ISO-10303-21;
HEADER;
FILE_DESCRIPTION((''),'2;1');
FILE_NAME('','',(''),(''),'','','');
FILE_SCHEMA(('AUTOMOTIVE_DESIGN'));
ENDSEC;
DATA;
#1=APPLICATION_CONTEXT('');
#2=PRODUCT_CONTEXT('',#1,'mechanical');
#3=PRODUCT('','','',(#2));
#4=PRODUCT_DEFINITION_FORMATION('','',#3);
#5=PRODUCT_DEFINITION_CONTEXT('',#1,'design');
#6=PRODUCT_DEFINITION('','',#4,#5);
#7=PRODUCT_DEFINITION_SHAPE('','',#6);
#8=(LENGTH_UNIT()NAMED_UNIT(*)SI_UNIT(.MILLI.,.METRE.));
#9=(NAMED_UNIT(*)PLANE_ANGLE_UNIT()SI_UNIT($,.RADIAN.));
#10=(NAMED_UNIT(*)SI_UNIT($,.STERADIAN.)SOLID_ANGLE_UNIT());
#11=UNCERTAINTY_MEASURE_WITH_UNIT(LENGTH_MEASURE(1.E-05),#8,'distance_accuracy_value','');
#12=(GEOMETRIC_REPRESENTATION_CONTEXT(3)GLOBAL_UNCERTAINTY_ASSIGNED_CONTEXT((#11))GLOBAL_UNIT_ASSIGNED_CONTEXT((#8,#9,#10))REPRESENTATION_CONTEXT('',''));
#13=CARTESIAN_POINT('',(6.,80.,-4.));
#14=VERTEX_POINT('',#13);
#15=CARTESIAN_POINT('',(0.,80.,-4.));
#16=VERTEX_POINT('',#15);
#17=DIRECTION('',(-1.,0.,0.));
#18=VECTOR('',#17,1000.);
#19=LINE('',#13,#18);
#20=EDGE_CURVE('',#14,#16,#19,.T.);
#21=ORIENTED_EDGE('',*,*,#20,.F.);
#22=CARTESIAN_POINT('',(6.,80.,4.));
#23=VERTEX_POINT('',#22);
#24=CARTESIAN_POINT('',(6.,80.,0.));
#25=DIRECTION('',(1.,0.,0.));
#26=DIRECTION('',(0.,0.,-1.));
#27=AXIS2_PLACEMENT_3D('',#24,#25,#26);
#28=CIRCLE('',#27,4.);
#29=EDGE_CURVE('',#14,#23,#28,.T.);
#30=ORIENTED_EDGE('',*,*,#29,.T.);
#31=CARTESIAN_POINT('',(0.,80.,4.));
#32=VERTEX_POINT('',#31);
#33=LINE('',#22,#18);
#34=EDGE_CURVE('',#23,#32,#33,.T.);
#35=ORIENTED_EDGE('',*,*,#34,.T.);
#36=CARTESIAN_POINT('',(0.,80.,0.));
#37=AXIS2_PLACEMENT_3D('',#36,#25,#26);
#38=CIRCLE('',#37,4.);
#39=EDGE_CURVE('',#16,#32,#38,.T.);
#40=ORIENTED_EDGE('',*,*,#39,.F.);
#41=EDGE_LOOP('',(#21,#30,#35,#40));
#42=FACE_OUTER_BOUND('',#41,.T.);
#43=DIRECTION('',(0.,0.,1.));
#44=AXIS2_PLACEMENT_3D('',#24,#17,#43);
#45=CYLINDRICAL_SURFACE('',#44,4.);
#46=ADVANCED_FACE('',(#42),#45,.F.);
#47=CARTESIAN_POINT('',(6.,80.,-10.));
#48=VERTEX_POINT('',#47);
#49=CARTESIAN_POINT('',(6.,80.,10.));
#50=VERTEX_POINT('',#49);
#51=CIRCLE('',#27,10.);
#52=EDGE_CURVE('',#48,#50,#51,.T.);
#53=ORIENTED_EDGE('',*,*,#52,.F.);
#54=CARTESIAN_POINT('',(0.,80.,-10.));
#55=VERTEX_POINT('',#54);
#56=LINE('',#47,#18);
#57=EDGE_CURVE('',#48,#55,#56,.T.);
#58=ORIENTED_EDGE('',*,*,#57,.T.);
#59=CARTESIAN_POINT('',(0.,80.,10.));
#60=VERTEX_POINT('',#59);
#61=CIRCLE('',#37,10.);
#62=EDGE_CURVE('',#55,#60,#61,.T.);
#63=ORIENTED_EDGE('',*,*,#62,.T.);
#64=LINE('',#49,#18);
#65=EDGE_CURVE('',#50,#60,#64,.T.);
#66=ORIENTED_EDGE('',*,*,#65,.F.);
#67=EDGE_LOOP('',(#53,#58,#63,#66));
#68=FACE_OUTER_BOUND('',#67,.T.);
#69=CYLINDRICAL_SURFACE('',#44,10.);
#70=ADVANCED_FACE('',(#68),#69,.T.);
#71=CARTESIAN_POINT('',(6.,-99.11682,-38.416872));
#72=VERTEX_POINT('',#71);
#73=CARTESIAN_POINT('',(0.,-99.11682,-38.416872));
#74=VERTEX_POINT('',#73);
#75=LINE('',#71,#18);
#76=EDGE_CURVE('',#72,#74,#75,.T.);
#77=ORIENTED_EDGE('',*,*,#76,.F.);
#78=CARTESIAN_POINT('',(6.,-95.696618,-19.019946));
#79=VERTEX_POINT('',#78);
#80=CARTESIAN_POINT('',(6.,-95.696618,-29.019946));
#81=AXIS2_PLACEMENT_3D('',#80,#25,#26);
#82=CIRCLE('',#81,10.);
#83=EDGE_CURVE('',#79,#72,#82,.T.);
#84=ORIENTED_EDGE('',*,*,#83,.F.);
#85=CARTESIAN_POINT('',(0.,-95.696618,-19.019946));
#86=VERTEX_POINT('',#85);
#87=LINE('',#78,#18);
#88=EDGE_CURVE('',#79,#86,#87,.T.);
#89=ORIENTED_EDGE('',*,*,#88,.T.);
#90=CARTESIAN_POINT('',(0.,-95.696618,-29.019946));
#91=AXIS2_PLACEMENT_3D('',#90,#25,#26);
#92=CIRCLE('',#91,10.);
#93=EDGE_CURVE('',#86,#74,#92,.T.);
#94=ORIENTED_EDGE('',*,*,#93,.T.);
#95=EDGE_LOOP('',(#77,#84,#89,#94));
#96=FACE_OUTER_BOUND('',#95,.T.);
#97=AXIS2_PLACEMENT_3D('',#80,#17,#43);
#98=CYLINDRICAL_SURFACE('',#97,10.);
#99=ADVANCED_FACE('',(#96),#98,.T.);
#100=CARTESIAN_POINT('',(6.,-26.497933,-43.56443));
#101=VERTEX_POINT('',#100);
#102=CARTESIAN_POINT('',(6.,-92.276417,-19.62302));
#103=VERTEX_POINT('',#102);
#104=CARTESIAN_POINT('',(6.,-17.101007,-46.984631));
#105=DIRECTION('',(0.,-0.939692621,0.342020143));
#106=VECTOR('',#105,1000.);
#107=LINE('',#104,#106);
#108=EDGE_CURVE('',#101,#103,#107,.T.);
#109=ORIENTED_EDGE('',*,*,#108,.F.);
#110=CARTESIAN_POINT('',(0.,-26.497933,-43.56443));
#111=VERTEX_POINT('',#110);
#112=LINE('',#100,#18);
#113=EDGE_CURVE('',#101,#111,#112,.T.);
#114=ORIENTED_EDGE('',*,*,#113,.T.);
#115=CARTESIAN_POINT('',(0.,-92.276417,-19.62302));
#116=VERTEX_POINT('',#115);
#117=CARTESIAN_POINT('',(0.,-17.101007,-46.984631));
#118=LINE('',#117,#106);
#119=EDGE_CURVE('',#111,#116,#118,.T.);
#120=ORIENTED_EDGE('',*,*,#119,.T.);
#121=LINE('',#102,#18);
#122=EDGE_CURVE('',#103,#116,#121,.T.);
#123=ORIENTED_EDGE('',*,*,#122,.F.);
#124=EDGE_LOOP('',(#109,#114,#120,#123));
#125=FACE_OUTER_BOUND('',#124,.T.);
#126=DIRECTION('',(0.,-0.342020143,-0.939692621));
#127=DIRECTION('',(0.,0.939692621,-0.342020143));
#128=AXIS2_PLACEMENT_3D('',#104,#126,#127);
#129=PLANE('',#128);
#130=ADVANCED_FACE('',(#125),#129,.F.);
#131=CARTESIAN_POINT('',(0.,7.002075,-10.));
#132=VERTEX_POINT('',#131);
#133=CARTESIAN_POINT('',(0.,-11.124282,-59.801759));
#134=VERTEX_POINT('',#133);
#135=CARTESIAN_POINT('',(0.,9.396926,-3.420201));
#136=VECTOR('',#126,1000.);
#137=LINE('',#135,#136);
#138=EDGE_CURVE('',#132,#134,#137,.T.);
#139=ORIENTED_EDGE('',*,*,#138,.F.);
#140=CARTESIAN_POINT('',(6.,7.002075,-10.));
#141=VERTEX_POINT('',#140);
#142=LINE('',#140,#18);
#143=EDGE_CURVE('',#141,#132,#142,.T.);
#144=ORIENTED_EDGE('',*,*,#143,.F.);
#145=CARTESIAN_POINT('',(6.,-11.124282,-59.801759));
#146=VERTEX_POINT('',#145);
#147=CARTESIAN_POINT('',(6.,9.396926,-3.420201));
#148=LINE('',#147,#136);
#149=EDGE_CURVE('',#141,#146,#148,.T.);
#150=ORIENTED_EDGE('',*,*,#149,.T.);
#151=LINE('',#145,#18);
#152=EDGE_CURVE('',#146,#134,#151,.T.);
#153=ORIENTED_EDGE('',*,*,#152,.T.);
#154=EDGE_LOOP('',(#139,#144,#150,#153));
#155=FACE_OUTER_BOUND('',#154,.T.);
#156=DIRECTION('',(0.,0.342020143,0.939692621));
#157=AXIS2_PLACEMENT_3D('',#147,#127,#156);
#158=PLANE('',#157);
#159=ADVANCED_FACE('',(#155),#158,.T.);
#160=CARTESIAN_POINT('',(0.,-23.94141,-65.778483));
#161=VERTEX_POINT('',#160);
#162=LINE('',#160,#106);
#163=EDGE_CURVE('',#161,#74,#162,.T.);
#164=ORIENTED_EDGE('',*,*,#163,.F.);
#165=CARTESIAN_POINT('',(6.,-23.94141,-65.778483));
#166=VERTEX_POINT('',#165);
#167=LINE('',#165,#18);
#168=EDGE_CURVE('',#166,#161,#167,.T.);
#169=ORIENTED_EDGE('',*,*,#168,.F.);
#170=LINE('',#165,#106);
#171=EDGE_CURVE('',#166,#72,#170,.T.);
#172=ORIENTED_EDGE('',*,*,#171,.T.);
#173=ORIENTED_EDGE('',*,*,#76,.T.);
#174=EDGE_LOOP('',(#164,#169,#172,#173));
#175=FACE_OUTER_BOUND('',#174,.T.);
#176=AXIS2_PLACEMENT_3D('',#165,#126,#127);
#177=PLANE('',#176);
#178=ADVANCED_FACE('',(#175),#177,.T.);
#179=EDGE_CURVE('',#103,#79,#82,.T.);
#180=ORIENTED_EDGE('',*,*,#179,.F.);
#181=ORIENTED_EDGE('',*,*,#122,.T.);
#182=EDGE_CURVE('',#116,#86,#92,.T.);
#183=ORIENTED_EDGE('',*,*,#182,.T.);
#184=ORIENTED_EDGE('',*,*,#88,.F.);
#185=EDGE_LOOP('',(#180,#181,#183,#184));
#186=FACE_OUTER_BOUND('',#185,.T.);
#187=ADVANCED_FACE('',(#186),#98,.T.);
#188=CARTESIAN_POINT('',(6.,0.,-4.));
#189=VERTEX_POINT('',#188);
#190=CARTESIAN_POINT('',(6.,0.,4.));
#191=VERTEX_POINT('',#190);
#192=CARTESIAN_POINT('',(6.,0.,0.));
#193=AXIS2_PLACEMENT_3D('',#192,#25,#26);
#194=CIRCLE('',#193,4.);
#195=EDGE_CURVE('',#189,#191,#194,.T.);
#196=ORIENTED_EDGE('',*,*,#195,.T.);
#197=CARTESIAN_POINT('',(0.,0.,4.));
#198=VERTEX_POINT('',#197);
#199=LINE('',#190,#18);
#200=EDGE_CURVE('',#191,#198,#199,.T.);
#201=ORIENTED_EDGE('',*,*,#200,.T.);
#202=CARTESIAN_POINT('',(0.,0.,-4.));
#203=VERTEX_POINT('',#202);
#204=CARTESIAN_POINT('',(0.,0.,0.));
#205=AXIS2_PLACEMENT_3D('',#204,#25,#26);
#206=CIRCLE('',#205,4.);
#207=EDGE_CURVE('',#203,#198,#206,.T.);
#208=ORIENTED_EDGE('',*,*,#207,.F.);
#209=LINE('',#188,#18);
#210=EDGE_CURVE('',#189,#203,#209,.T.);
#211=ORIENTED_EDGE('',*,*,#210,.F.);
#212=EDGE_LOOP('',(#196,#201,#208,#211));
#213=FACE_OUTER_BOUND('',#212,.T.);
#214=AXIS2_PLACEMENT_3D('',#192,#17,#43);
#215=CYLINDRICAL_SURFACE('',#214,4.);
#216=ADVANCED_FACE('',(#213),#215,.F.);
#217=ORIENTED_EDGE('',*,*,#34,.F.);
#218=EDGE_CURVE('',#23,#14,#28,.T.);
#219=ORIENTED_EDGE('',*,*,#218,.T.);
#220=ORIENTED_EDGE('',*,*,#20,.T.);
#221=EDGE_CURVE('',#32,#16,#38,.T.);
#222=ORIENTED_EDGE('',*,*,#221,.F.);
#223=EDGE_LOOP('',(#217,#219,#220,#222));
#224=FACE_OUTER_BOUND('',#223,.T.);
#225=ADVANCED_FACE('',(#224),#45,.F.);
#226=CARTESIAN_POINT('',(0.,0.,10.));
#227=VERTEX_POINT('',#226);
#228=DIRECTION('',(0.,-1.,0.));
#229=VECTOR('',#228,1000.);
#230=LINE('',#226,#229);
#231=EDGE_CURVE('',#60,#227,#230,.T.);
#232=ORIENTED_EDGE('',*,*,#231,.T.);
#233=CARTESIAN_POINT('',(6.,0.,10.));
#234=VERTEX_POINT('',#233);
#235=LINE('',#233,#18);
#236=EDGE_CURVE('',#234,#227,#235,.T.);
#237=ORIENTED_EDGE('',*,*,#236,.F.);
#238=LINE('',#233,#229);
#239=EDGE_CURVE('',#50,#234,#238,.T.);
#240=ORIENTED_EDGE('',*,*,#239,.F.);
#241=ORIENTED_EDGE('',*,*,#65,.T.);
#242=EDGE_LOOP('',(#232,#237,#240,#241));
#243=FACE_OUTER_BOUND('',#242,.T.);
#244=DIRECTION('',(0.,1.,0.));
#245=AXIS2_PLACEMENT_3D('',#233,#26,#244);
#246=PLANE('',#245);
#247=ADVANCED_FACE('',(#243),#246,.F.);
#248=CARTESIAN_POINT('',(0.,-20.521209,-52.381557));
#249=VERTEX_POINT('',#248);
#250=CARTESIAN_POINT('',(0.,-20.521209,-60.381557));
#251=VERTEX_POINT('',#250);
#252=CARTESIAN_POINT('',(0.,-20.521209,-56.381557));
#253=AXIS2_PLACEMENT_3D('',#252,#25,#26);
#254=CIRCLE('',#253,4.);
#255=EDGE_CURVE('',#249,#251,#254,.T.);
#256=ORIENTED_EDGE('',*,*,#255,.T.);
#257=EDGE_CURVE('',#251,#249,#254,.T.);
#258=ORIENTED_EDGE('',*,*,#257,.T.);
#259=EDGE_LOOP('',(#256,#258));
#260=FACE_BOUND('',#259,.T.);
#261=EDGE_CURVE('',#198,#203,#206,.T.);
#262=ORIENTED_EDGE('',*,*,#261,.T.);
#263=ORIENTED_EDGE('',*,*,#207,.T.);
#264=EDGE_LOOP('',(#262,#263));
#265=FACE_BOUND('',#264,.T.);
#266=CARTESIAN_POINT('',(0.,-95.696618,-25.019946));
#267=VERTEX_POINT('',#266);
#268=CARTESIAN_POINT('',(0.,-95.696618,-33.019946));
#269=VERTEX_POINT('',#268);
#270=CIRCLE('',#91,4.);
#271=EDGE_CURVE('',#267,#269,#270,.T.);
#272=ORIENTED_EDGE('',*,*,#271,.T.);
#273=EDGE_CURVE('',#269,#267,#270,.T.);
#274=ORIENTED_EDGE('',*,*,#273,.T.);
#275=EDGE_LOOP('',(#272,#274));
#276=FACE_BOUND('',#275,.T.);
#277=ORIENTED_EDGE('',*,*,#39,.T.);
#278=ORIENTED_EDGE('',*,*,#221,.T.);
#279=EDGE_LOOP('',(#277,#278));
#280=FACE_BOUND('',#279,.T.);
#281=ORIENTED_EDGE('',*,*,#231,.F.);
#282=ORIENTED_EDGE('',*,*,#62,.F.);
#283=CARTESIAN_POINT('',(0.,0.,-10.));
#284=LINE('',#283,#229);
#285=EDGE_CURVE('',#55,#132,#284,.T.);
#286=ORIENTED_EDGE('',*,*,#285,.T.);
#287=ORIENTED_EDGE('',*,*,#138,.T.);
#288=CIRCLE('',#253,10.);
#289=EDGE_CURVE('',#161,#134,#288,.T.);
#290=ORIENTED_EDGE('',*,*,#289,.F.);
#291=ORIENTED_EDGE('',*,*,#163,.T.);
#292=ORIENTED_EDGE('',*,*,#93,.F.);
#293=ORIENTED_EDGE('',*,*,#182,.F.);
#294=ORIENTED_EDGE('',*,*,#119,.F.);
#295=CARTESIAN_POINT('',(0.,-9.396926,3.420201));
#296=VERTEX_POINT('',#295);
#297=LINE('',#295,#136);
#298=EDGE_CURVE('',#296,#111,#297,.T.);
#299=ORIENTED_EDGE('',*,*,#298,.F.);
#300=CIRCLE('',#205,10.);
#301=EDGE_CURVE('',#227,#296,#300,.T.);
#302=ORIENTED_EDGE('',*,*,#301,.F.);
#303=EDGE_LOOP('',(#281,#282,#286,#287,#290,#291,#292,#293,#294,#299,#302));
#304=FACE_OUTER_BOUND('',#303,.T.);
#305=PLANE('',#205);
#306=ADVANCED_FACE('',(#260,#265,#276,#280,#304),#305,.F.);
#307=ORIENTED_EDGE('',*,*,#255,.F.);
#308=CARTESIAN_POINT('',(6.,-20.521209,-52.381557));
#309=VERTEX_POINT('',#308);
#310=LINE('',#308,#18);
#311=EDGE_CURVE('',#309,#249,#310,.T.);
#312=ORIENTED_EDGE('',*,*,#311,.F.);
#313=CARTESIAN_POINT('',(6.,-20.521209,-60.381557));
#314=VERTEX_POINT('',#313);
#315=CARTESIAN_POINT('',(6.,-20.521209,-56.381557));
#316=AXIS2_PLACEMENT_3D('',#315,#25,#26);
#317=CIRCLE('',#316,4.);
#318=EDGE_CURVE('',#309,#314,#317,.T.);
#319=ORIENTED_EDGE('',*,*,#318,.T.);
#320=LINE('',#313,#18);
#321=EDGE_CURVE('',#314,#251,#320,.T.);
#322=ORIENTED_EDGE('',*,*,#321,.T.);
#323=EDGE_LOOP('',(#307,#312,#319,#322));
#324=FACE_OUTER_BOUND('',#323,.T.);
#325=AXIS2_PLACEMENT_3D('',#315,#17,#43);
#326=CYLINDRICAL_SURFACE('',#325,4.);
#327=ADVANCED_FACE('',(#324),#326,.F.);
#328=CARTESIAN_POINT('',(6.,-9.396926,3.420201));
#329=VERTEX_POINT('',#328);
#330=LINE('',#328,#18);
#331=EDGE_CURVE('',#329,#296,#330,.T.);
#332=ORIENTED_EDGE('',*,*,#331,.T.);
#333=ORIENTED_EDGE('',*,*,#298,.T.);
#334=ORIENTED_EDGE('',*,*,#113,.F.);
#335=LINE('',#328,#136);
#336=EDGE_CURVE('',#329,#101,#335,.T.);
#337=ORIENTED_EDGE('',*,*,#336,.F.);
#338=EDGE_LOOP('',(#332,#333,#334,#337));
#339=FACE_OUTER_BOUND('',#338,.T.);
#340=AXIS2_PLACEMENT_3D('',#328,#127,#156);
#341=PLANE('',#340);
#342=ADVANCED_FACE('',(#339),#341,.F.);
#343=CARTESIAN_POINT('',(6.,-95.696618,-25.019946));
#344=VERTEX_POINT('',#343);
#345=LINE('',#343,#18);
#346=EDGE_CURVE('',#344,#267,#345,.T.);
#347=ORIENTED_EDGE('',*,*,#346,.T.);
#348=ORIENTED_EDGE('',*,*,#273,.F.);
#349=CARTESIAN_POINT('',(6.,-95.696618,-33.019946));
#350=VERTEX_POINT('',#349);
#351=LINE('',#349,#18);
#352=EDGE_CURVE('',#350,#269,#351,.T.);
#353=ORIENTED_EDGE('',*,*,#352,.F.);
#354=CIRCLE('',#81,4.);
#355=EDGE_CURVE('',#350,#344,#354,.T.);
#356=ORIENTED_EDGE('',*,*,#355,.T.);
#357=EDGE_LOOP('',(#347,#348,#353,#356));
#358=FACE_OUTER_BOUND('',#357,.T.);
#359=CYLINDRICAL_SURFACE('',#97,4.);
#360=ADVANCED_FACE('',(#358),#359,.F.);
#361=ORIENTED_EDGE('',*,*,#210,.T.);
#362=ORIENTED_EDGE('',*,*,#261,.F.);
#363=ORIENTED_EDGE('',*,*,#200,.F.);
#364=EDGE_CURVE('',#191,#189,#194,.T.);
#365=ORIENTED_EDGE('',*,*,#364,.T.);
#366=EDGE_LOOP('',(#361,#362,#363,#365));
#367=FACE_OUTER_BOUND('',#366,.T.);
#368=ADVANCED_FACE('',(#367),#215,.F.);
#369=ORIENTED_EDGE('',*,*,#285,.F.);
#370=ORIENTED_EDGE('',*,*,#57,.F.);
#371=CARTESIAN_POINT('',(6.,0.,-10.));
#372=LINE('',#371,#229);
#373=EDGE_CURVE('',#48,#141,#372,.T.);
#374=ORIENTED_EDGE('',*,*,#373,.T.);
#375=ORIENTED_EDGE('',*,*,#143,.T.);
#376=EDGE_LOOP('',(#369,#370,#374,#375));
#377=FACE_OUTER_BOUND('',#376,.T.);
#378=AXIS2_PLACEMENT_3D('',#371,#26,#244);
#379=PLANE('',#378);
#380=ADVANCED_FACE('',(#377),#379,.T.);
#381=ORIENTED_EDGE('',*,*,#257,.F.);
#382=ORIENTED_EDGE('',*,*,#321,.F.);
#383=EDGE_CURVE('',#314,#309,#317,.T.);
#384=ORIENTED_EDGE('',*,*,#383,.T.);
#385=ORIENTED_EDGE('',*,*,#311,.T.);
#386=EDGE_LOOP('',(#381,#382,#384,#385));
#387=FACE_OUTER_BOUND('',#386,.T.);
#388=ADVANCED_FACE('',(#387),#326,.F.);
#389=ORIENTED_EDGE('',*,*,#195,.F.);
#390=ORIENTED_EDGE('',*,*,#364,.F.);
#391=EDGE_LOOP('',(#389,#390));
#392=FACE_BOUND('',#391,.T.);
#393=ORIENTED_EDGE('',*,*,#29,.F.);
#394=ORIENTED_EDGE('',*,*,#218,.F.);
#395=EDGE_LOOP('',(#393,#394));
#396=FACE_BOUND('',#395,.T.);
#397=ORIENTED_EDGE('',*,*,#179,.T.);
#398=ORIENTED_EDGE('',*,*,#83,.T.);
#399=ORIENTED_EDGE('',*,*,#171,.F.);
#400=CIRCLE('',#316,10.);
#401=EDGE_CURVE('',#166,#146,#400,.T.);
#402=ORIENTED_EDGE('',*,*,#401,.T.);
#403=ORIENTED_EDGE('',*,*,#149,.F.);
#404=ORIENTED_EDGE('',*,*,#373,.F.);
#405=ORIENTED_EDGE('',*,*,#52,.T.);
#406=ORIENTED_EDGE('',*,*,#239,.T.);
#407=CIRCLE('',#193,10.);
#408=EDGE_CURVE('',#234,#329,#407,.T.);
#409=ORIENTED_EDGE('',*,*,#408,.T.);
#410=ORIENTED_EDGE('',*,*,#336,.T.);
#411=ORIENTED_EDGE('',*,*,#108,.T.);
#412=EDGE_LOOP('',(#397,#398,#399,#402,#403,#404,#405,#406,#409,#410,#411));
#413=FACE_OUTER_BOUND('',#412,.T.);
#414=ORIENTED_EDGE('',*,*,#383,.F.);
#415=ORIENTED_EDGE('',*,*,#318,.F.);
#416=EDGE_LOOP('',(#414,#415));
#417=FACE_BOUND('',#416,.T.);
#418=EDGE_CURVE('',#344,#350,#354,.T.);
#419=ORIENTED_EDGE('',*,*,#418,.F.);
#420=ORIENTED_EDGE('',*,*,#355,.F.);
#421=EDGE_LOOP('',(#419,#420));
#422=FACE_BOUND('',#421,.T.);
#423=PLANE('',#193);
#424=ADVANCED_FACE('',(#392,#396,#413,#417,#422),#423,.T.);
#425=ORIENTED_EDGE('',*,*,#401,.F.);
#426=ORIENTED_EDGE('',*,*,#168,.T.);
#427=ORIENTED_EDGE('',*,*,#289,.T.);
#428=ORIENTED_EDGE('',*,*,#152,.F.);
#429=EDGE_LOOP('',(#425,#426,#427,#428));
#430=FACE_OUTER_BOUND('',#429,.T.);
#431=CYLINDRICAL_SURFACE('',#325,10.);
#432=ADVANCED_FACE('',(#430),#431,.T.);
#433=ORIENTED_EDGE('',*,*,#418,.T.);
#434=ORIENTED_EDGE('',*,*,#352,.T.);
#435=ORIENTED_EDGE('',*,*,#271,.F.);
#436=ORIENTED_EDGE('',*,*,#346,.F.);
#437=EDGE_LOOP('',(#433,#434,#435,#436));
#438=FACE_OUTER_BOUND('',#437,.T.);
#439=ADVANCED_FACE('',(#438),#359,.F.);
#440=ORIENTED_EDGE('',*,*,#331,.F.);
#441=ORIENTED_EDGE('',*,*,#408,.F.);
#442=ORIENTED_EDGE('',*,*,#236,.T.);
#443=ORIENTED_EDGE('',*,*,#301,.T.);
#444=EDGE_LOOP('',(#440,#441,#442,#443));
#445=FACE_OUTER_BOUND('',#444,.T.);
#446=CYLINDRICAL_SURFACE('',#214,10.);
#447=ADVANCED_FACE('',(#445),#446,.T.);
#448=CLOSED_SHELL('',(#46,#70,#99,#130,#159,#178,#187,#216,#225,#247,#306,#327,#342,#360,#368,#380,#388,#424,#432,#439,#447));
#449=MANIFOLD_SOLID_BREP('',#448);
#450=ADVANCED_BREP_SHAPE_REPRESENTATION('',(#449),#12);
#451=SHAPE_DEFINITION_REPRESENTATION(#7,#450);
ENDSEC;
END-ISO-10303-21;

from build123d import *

# Parameters (mm, degrees)
SKETCH1_R           = 4
BOSS_EXTRUDE1_DEPTH = 6


with BuildPart() as part:
    # Sketch1 → Boss-Extrude1 (new body)
    # profile 1 of 5: a face of its own
    with BuildSketch(Plane(origin=(0, 0, 0), x_dir=(0, 0, -1), z_dir=(1, 0, 0))):
        with BuildLine():
            Line((38.416871989, -99.116819696), (65.778483455, -23.941410033))
            ThreePointArc((65.778483455, -23.941410033), (60.607739865, -29.58428647), (52.961355814, -29.918134807))
            Line((52.961355814, -29.918134807), (43.564429606, -26.497933374))
            Line((43.564429606, -26.497933374), (19.623019573, -92.276416829))
            ThreePointArc((19.623019573, -92.276416829), (25.599744348, -105.09354447), (38.416871989, -99.116819696))
        make_face()
        with Locations((29.019945781, -95.696618262)):
            Circle(SKETCH1_R, mode=Mode.SUBTRACT)
    # profile 2 of 5: a face of its own
    with BuildSketch(Plane(origin=(0, 0, 0), x_dir=(0, 0, -1), z_dir=(1, 0, 0))):
        with BuildLine():
            ThreePointArc((65.778483455, -23.941410033), (65.444635118, -16.295025982), (59.80175868, -11.124282392))
            ThreePointArc((59.80175868, -11.124282392), (52.15537463, -11.458130729), (46.984631039, -17.101007166))
            Line((46.984631039, -17.101007166), (43.564429606, -26.497933374))
            Line((43.564429606, -26.497933374), (52.961355814, -29.918134807))
            ThreePointArc((52.961355814, -29.918134807), (60.607739865, -29.58428647), (65.778483455, -23.941410033))
        make_face()
        with Locations((56.381557247, -20.5212086)):
            Circle(SKETCH1_R, mode=Mode.SUBTRACT)
    # profile 3 of 5: a face of its own
    with BuildSketch(Plane(origin=(0, 0, 0), x_dir=(0, 0, -1), z_dir=(1, 0, 0))):
        with BuildLine():
            Line((59.80175868, -11.124282392), (10, 7.002075382))
            Line((10, 7.002075382), (10, 0))
            ThreePointArc((10, 0), (5.735764364, -8.191520443), (-3.420201433, -9.396926208))
            Line((-3.420201433, -9.396926208), (43.564429606, -26.497933374))
            Line((43.564429606, -26.497933374), (46.984631039, -17.101007166))
            ThreePointArc((46.984631039, -17.101007166), (52.15537463, -11.458130729), (59.80175868, -11.124282392))
        make_face()
    # profile 4 of 5: a face of its own
    with BuildSketch(Plane(origin=(0, 0, 0), x_dir=(0, 0, -1), z_dir=(1, 0, 0))):
        with BuildLine():
            Line((10, 0), (10, 7.002075382))
            Line((10, 7.002075382), (3.420201433, 9.396926208))
            ThreePointArc((3.420201433, 9.396926208), (-5.735764364, 8.191520443), (-10, 0))
            ThreePointArc((-10, 0), (-8.191520443, -5.735764364), (-3.420201433, -9.396926208))
            ThreePointArc((-3.420201433, -9.396926208), (5.735764364, -8.191520443), (10, 0))
        make_face()
        Circle(SKETCH1_R, mode=Mode.SUBTRACT)
    # profile 5 of 5: a face of its own
    with BuildSketch(Plane(origin=(0, 0, 0), x_dir=(0, 0, -1), z_dir=(1, 0, 0))):
        with BuildLine():
            Line((10, 7.002075382), (10, 80))
            ThreePointArc((10, 80), (0, 90), (-10, 80))
            Line((-10, 80), (-10, 0))
            ThreePointArc((-10, 0), (-5.735764364, 8.191520443), (3.420201433, 9.396926208))
            Line((3.420201433, 9.396926208), (10, 7.002075382))
        make_face()
        with Locations((0, 80)):
            Circle(SKETCH1_R, mode=Mode.SUBTRACT)
    extrude(amount=BOSS_EXTRUDE1_DEPTH)


solid = part.part
